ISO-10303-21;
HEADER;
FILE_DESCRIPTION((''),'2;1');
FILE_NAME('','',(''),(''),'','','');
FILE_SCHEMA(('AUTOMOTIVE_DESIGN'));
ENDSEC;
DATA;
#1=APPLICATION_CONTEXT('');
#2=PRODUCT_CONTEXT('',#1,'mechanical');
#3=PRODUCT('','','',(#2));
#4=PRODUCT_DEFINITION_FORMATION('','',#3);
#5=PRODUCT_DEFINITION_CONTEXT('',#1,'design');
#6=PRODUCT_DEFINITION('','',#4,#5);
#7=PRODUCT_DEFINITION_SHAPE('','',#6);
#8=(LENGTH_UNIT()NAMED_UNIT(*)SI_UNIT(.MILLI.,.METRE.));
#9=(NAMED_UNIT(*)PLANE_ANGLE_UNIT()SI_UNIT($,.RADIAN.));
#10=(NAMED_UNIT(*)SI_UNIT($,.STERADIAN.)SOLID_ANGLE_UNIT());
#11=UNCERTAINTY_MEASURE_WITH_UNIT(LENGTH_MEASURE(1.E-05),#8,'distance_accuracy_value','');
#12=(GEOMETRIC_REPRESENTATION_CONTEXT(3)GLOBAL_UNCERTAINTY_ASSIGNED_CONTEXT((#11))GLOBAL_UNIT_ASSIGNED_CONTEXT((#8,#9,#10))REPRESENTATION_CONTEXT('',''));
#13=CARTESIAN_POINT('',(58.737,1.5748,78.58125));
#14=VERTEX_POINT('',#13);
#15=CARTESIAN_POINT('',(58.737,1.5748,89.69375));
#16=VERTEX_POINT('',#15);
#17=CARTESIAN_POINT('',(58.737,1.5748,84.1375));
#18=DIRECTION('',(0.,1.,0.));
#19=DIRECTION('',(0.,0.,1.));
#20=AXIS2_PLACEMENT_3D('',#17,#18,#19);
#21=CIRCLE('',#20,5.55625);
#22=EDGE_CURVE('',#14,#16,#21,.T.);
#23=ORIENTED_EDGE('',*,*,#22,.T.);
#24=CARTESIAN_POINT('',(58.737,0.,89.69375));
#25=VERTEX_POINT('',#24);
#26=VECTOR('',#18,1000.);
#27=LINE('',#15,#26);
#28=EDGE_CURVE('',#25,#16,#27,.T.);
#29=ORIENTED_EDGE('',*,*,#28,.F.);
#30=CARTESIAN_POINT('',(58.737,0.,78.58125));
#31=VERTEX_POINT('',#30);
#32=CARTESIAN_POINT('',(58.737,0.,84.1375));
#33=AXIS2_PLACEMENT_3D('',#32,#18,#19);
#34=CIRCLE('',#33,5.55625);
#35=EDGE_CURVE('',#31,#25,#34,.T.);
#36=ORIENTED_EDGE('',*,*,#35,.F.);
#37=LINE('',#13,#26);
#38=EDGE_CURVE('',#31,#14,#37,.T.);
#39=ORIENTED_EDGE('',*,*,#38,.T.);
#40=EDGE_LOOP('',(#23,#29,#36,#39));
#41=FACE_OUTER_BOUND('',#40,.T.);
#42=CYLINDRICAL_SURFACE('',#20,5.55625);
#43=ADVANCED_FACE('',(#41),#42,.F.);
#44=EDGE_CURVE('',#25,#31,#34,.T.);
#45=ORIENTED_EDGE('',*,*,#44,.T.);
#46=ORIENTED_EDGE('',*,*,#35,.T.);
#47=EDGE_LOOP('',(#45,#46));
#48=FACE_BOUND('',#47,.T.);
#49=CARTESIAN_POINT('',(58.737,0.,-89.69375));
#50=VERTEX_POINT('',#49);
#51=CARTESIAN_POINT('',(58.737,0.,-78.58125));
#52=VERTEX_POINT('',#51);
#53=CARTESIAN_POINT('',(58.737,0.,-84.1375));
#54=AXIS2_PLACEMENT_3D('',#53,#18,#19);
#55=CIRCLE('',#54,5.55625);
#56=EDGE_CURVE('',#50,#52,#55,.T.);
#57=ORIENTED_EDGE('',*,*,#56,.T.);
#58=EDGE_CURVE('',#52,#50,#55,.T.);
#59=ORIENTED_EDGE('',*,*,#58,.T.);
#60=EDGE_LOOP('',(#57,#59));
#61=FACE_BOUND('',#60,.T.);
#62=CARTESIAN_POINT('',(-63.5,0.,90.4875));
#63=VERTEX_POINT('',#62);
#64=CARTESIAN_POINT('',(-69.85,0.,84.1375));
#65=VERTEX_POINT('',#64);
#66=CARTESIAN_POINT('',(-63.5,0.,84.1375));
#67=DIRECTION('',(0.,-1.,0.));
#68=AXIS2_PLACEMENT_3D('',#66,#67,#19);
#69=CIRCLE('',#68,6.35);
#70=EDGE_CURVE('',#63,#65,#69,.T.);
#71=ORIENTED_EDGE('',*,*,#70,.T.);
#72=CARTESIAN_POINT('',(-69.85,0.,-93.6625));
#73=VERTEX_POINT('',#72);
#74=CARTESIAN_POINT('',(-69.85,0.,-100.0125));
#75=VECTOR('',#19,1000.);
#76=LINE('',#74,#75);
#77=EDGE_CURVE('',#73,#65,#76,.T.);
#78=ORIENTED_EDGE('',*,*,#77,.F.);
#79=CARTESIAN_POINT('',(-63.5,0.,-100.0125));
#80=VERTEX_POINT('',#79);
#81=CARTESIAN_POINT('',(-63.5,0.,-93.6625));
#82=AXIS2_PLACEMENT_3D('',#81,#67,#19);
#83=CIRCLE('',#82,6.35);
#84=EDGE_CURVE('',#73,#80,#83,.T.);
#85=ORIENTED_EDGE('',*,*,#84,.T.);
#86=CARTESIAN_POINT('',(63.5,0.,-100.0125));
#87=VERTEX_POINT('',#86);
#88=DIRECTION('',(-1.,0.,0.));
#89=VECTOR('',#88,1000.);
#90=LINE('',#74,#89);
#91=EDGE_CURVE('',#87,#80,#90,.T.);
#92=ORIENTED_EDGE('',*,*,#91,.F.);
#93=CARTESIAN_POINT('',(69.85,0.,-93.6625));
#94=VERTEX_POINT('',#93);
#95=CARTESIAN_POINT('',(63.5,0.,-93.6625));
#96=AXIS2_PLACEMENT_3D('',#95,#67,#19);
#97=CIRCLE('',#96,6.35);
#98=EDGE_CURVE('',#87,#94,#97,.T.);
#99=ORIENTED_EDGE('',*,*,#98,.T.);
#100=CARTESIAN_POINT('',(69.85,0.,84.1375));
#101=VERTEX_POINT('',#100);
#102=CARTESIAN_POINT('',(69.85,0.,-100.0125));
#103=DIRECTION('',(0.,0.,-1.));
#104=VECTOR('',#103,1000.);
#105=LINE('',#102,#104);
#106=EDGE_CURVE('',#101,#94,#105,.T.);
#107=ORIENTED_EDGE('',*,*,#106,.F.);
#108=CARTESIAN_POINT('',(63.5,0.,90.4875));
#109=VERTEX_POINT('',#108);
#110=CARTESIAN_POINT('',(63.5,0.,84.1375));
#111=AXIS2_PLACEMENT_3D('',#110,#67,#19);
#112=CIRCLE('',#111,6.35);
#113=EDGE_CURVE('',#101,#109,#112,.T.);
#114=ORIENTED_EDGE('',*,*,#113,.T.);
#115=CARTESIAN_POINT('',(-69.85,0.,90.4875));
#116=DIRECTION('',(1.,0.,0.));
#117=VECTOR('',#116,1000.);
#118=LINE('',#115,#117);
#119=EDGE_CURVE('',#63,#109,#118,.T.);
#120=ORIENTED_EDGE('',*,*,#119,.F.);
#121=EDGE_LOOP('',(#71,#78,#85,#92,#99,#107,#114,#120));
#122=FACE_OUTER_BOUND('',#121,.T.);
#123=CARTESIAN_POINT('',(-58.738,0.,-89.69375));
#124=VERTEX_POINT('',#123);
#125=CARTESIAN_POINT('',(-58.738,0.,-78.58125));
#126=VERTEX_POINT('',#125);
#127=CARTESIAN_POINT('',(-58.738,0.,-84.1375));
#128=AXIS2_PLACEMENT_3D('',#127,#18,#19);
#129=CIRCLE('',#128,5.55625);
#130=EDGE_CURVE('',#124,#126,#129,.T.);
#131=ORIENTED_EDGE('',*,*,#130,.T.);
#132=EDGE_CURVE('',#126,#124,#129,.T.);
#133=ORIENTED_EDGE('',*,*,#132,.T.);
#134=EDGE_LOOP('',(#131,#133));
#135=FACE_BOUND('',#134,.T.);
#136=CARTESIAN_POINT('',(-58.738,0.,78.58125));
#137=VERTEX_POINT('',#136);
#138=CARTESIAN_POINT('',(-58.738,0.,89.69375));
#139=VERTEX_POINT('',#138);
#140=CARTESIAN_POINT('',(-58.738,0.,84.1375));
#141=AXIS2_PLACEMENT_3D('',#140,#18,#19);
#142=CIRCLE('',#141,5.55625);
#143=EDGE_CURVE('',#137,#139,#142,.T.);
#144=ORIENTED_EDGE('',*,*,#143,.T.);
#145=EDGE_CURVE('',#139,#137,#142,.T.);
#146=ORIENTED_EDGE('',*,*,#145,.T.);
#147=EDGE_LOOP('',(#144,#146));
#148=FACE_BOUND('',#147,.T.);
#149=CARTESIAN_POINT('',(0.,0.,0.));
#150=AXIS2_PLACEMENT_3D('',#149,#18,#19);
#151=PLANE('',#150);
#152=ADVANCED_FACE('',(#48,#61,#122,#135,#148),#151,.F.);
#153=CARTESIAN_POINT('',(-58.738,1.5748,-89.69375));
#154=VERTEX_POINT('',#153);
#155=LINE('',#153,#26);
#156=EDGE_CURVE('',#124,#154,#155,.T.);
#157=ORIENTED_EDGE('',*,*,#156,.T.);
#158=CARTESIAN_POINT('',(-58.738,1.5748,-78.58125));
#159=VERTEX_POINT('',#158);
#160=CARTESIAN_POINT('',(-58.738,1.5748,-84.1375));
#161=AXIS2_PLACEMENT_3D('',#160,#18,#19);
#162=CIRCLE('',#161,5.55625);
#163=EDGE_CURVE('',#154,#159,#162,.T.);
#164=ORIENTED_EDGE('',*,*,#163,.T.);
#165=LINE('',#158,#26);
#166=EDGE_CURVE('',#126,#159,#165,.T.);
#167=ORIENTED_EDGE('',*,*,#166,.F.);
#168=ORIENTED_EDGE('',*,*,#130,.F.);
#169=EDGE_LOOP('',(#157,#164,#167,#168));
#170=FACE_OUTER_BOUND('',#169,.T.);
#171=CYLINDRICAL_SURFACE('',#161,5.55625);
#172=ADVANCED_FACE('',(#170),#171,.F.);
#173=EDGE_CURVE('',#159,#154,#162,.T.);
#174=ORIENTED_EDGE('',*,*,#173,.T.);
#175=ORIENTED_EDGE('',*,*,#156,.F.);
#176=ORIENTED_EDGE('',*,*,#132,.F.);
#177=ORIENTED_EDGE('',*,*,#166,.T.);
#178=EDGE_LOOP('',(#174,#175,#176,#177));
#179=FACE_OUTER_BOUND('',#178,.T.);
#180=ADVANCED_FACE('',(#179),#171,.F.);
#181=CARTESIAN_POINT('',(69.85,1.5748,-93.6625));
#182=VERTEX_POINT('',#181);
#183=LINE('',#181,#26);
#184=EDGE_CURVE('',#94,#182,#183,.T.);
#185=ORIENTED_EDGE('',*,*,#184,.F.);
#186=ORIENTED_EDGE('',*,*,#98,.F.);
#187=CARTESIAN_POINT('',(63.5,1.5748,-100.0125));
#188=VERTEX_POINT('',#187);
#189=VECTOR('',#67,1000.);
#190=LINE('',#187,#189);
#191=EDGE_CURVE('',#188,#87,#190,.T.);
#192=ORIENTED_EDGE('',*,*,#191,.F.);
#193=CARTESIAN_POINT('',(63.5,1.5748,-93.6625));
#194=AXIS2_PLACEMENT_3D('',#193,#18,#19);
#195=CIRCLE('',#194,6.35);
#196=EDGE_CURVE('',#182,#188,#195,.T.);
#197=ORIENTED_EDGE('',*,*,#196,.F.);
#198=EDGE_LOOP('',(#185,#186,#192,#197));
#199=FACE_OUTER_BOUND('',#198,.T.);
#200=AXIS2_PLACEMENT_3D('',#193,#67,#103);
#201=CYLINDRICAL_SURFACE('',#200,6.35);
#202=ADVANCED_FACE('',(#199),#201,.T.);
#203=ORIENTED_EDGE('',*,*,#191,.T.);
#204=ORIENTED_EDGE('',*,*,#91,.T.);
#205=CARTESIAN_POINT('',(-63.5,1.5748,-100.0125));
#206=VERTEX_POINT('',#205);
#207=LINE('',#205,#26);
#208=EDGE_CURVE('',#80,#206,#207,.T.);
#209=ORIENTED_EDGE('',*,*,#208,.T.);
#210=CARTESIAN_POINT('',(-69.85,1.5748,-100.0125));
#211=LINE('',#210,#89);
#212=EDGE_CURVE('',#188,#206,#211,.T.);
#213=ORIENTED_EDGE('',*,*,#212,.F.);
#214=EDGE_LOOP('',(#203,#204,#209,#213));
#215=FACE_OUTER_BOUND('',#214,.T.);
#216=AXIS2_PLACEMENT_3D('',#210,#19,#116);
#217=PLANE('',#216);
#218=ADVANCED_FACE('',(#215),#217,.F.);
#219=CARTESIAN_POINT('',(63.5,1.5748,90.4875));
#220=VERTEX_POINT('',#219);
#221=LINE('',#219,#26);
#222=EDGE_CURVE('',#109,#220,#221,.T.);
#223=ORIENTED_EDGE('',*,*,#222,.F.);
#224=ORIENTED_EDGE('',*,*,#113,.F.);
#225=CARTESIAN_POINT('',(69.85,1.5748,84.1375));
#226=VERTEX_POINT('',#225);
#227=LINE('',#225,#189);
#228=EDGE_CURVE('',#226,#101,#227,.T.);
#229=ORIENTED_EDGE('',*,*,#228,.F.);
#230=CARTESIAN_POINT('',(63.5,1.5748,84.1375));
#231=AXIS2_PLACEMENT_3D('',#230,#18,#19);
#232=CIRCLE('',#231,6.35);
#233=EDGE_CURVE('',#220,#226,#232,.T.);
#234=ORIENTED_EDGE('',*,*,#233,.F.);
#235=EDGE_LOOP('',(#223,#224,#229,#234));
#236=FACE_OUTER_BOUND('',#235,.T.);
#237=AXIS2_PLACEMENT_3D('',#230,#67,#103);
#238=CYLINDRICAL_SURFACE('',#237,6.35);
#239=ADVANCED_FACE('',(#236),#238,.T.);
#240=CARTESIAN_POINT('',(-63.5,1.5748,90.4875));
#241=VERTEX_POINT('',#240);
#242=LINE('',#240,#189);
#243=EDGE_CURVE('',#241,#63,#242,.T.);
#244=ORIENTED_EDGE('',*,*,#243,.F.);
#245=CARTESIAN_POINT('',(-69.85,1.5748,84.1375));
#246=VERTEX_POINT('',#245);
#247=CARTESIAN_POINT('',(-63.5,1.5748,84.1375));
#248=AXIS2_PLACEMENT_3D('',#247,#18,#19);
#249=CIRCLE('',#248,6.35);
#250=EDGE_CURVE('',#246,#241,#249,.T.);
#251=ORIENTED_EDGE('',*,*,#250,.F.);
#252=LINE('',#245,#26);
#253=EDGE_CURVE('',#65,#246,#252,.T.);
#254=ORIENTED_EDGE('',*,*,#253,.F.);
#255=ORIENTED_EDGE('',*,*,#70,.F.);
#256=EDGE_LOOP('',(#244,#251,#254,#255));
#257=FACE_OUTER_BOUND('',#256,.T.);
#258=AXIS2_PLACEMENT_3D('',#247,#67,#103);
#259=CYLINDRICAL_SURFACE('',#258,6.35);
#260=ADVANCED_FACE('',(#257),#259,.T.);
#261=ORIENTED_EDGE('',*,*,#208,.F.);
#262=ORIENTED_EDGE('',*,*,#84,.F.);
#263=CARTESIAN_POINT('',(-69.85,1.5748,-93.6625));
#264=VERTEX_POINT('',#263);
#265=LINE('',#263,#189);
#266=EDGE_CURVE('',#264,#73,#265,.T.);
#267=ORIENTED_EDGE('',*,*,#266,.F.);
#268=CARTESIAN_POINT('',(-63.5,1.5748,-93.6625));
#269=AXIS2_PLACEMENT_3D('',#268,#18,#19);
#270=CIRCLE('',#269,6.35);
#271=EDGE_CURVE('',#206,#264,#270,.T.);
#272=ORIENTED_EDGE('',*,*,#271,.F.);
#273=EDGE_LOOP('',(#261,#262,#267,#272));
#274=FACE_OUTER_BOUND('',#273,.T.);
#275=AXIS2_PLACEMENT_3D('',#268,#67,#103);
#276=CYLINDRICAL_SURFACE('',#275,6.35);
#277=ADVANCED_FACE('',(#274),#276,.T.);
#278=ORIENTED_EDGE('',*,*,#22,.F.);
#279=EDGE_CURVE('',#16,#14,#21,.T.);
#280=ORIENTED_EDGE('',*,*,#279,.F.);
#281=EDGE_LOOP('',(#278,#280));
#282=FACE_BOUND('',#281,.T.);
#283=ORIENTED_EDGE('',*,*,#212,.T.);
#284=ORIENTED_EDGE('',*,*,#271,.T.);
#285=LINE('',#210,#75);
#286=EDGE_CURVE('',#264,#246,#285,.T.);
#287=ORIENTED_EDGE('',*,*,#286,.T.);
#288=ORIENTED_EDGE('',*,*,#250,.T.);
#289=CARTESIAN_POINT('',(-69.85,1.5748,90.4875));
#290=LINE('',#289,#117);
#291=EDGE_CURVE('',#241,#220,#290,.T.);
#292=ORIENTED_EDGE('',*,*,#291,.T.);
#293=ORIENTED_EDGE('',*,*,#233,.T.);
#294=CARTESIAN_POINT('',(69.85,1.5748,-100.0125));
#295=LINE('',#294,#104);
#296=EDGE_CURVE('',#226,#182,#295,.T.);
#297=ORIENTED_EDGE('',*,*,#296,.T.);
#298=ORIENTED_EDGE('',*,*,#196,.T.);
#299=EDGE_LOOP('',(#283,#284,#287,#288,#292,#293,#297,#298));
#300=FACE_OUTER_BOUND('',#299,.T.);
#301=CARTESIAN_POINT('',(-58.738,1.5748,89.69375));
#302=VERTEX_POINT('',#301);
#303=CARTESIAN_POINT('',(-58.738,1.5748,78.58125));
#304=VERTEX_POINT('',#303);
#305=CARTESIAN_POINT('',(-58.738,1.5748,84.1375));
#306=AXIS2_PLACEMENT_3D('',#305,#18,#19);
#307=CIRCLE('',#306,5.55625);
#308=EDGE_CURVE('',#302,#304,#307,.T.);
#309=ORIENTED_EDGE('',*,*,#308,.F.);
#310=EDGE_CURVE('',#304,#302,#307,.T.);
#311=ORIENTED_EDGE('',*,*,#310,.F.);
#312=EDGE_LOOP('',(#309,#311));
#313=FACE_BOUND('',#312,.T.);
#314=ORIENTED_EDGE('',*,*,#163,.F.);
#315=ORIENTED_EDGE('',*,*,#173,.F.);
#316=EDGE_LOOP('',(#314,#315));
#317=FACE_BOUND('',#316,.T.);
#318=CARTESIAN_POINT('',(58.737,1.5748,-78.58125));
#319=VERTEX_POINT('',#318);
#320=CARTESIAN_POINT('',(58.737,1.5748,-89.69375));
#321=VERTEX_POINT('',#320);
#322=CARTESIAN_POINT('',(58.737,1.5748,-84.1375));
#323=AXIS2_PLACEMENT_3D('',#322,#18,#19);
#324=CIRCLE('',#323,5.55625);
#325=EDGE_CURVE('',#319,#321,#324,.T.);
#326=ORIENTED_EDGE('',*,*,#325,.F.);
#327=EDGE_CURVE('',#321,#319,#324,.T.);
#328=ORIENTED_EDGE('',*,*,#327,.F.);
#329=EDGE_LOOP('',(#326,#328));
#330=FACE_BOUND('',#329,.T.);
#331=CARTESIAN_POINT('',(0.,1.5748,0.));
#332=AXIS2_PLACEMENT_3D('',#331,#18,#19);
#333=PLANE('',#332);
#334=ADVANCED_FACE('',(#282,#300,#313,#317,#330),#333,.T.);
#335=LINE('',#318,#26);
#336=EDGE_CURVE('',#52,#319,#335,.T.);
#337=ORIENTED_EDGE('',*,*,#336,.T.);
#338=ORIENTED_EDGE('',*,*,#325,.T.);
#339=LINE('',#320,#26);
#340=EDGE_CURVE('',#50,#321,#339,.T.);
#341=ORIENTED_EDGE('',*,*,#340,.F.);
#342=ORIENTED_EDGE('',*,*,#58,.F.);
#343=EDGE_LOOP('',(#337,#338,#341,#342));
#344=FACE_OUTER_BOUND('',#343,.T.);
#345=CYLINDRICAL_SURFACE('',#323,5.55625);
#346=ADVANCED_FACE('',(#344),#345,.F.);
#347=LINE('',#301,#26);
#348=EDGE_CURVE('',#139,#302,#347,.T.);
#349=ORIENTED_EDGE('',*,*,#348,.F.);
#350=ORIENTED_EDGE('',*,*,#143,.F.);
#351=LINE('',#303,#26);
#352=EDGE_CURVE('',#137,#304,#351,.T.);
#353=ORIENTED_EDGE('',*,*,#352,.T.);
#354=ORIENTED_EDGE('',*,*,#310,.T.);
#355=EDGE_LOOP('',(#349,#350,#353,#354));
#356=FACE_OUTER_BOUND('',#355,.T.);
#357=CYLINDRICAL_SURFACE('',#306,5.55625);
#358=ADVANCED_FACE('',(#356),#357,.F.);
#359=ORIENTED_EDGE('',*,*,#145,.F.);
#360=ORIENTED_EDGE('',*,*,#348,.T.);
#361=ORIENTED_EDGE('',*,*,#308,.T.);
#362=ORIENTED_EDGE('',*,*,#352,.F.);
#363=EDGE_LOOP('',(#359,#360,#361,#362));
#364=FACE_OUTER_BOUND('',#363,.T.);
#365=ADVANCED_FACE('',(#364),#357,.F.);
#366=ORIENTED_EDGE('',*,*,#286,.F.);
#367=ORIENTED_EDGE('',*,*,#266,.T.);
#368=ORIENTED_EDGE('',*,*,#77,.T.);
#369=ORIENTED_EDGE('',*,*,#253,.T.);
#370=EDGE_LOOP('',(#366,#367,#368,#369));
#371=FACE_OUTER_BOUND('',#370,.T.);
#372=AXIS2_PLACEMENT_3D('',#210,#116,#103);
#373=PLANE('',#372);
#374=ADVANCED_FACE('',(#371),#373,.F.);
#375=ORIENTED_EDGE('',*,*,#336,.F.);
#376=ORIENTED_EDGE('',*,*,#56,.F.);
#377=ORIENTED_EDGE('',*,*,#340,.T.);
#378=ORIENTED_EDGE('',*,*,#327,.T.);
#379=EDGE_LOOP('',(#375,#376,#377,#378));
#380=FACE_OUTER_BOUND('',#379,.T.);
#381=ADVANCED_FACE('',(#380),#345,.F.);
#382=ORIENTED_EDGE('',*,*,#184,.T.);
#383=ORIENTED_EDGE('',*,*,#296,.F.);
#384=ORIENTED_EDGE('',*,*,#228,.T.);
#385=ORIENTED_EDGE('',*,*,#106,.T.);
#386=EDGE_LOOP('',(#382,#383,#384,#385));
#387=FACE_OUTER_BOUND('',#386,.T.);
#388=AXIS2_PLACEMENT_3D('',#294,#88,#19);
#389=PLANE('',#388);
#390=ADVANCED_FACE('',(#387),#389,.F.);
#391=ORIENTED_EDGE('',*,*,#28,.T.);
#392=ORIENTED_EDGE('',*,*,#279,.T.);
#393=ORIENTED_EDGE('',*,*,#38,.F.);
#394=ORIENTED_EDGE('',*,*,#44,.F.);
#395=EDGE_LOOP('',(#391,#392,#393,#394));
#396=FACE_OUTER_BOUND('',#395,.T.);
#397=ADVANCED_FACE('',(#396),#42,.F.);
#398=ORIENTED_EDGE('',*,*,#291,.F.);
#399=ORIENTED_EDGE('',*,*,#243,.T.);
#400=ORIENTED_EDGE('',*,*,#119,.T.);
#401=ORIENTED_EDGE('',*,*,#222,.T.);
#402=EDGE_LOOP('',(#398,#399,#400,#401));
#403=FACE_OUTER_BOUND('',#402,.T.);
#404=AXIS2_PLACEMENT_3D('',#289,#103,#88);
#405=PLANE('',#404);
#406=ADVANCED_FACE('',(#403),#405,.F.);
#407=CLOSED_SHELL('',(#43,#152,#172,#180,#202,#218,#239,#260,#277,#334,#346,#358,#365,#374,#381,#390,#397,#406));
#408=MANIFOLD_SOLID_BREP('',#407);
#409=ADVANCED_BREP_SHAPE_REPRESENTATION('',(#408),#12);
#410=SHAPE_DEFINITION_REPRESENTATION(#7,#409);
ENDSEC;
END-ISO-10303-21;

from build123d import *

# Parameters (mm, degrees)
SKETCH1_W                      = 139.7
SKETCH1_H                      = 190.5
BOSS_EXTRUDE1_DEPTH            = 1.5748
FILLET1_R                      = 6.35
F_7_16_0_4375_DIAMETER_HOLE1_D = 11.1125
LPATTERN1_COUNT                = 2
LPATTERN1_PITCH                = 168.275
LPATTERN1_COUNT_DIR2           = 2
LPATTERN1_PITCH_DIR2           = 117.475


with BuildPart() as part:
    # Sketch1 → Boss-Extrude1 (new body)
    with BuildSketch(Plane(origin=(0, 0, 0), x_dir=(1, 0, 0), z_dir=(0, 1, 0))):
        with Locations((0, 4.7625)):
            Rectangle(SKETCH1_W, SKETCH1_H)
    extrude(amount=BOSS_EXTRUDE1_DEPTH)

    # Fillet1
    fillet1_edges = [part.edges().sort_by_distance(p)[0] for p in [
        (-69.85, 0.7874, -100.0125),
        (69.85, 0.7874, -100.0125),
        (69.85, 0.7874, 90.4875),
        (-69.85, 0.7874, 90.4875),
    ]]
    fillet(fillet1_edges, radius=FILLET1_R)

    # 7/16 (0.4375) Diameter Hole1 (through all)
    with Locations(Plane(origin=(0, 1.5748, 0), x_dir=(1, 0, 0), z_dir=(0, 1, 0))):
        with Locations((-58.738, 84.1375)):
            f_7_16_0_4375_diameter_hole1 = Hole(F_7_16_0_4375_DIAMETER_HOLE1_D / 2)

    # LPattern1: 7_16 _0.4375_ Diameter Hole1 2 × 2
    with Locations(*[(j * LPATTERN1_PITCH_DIR2, 0, i * LPATTERN1_PITCH) for i in range(LPATTERN1_COUNT) for j in range(LPATTERN1_COUNT_DIR2) if (i, j) != (0, 0)]):
        add(f_7_16_0_4375_diameter_hole1, mode=Mode.SUBTRACT)


solid = part.part
